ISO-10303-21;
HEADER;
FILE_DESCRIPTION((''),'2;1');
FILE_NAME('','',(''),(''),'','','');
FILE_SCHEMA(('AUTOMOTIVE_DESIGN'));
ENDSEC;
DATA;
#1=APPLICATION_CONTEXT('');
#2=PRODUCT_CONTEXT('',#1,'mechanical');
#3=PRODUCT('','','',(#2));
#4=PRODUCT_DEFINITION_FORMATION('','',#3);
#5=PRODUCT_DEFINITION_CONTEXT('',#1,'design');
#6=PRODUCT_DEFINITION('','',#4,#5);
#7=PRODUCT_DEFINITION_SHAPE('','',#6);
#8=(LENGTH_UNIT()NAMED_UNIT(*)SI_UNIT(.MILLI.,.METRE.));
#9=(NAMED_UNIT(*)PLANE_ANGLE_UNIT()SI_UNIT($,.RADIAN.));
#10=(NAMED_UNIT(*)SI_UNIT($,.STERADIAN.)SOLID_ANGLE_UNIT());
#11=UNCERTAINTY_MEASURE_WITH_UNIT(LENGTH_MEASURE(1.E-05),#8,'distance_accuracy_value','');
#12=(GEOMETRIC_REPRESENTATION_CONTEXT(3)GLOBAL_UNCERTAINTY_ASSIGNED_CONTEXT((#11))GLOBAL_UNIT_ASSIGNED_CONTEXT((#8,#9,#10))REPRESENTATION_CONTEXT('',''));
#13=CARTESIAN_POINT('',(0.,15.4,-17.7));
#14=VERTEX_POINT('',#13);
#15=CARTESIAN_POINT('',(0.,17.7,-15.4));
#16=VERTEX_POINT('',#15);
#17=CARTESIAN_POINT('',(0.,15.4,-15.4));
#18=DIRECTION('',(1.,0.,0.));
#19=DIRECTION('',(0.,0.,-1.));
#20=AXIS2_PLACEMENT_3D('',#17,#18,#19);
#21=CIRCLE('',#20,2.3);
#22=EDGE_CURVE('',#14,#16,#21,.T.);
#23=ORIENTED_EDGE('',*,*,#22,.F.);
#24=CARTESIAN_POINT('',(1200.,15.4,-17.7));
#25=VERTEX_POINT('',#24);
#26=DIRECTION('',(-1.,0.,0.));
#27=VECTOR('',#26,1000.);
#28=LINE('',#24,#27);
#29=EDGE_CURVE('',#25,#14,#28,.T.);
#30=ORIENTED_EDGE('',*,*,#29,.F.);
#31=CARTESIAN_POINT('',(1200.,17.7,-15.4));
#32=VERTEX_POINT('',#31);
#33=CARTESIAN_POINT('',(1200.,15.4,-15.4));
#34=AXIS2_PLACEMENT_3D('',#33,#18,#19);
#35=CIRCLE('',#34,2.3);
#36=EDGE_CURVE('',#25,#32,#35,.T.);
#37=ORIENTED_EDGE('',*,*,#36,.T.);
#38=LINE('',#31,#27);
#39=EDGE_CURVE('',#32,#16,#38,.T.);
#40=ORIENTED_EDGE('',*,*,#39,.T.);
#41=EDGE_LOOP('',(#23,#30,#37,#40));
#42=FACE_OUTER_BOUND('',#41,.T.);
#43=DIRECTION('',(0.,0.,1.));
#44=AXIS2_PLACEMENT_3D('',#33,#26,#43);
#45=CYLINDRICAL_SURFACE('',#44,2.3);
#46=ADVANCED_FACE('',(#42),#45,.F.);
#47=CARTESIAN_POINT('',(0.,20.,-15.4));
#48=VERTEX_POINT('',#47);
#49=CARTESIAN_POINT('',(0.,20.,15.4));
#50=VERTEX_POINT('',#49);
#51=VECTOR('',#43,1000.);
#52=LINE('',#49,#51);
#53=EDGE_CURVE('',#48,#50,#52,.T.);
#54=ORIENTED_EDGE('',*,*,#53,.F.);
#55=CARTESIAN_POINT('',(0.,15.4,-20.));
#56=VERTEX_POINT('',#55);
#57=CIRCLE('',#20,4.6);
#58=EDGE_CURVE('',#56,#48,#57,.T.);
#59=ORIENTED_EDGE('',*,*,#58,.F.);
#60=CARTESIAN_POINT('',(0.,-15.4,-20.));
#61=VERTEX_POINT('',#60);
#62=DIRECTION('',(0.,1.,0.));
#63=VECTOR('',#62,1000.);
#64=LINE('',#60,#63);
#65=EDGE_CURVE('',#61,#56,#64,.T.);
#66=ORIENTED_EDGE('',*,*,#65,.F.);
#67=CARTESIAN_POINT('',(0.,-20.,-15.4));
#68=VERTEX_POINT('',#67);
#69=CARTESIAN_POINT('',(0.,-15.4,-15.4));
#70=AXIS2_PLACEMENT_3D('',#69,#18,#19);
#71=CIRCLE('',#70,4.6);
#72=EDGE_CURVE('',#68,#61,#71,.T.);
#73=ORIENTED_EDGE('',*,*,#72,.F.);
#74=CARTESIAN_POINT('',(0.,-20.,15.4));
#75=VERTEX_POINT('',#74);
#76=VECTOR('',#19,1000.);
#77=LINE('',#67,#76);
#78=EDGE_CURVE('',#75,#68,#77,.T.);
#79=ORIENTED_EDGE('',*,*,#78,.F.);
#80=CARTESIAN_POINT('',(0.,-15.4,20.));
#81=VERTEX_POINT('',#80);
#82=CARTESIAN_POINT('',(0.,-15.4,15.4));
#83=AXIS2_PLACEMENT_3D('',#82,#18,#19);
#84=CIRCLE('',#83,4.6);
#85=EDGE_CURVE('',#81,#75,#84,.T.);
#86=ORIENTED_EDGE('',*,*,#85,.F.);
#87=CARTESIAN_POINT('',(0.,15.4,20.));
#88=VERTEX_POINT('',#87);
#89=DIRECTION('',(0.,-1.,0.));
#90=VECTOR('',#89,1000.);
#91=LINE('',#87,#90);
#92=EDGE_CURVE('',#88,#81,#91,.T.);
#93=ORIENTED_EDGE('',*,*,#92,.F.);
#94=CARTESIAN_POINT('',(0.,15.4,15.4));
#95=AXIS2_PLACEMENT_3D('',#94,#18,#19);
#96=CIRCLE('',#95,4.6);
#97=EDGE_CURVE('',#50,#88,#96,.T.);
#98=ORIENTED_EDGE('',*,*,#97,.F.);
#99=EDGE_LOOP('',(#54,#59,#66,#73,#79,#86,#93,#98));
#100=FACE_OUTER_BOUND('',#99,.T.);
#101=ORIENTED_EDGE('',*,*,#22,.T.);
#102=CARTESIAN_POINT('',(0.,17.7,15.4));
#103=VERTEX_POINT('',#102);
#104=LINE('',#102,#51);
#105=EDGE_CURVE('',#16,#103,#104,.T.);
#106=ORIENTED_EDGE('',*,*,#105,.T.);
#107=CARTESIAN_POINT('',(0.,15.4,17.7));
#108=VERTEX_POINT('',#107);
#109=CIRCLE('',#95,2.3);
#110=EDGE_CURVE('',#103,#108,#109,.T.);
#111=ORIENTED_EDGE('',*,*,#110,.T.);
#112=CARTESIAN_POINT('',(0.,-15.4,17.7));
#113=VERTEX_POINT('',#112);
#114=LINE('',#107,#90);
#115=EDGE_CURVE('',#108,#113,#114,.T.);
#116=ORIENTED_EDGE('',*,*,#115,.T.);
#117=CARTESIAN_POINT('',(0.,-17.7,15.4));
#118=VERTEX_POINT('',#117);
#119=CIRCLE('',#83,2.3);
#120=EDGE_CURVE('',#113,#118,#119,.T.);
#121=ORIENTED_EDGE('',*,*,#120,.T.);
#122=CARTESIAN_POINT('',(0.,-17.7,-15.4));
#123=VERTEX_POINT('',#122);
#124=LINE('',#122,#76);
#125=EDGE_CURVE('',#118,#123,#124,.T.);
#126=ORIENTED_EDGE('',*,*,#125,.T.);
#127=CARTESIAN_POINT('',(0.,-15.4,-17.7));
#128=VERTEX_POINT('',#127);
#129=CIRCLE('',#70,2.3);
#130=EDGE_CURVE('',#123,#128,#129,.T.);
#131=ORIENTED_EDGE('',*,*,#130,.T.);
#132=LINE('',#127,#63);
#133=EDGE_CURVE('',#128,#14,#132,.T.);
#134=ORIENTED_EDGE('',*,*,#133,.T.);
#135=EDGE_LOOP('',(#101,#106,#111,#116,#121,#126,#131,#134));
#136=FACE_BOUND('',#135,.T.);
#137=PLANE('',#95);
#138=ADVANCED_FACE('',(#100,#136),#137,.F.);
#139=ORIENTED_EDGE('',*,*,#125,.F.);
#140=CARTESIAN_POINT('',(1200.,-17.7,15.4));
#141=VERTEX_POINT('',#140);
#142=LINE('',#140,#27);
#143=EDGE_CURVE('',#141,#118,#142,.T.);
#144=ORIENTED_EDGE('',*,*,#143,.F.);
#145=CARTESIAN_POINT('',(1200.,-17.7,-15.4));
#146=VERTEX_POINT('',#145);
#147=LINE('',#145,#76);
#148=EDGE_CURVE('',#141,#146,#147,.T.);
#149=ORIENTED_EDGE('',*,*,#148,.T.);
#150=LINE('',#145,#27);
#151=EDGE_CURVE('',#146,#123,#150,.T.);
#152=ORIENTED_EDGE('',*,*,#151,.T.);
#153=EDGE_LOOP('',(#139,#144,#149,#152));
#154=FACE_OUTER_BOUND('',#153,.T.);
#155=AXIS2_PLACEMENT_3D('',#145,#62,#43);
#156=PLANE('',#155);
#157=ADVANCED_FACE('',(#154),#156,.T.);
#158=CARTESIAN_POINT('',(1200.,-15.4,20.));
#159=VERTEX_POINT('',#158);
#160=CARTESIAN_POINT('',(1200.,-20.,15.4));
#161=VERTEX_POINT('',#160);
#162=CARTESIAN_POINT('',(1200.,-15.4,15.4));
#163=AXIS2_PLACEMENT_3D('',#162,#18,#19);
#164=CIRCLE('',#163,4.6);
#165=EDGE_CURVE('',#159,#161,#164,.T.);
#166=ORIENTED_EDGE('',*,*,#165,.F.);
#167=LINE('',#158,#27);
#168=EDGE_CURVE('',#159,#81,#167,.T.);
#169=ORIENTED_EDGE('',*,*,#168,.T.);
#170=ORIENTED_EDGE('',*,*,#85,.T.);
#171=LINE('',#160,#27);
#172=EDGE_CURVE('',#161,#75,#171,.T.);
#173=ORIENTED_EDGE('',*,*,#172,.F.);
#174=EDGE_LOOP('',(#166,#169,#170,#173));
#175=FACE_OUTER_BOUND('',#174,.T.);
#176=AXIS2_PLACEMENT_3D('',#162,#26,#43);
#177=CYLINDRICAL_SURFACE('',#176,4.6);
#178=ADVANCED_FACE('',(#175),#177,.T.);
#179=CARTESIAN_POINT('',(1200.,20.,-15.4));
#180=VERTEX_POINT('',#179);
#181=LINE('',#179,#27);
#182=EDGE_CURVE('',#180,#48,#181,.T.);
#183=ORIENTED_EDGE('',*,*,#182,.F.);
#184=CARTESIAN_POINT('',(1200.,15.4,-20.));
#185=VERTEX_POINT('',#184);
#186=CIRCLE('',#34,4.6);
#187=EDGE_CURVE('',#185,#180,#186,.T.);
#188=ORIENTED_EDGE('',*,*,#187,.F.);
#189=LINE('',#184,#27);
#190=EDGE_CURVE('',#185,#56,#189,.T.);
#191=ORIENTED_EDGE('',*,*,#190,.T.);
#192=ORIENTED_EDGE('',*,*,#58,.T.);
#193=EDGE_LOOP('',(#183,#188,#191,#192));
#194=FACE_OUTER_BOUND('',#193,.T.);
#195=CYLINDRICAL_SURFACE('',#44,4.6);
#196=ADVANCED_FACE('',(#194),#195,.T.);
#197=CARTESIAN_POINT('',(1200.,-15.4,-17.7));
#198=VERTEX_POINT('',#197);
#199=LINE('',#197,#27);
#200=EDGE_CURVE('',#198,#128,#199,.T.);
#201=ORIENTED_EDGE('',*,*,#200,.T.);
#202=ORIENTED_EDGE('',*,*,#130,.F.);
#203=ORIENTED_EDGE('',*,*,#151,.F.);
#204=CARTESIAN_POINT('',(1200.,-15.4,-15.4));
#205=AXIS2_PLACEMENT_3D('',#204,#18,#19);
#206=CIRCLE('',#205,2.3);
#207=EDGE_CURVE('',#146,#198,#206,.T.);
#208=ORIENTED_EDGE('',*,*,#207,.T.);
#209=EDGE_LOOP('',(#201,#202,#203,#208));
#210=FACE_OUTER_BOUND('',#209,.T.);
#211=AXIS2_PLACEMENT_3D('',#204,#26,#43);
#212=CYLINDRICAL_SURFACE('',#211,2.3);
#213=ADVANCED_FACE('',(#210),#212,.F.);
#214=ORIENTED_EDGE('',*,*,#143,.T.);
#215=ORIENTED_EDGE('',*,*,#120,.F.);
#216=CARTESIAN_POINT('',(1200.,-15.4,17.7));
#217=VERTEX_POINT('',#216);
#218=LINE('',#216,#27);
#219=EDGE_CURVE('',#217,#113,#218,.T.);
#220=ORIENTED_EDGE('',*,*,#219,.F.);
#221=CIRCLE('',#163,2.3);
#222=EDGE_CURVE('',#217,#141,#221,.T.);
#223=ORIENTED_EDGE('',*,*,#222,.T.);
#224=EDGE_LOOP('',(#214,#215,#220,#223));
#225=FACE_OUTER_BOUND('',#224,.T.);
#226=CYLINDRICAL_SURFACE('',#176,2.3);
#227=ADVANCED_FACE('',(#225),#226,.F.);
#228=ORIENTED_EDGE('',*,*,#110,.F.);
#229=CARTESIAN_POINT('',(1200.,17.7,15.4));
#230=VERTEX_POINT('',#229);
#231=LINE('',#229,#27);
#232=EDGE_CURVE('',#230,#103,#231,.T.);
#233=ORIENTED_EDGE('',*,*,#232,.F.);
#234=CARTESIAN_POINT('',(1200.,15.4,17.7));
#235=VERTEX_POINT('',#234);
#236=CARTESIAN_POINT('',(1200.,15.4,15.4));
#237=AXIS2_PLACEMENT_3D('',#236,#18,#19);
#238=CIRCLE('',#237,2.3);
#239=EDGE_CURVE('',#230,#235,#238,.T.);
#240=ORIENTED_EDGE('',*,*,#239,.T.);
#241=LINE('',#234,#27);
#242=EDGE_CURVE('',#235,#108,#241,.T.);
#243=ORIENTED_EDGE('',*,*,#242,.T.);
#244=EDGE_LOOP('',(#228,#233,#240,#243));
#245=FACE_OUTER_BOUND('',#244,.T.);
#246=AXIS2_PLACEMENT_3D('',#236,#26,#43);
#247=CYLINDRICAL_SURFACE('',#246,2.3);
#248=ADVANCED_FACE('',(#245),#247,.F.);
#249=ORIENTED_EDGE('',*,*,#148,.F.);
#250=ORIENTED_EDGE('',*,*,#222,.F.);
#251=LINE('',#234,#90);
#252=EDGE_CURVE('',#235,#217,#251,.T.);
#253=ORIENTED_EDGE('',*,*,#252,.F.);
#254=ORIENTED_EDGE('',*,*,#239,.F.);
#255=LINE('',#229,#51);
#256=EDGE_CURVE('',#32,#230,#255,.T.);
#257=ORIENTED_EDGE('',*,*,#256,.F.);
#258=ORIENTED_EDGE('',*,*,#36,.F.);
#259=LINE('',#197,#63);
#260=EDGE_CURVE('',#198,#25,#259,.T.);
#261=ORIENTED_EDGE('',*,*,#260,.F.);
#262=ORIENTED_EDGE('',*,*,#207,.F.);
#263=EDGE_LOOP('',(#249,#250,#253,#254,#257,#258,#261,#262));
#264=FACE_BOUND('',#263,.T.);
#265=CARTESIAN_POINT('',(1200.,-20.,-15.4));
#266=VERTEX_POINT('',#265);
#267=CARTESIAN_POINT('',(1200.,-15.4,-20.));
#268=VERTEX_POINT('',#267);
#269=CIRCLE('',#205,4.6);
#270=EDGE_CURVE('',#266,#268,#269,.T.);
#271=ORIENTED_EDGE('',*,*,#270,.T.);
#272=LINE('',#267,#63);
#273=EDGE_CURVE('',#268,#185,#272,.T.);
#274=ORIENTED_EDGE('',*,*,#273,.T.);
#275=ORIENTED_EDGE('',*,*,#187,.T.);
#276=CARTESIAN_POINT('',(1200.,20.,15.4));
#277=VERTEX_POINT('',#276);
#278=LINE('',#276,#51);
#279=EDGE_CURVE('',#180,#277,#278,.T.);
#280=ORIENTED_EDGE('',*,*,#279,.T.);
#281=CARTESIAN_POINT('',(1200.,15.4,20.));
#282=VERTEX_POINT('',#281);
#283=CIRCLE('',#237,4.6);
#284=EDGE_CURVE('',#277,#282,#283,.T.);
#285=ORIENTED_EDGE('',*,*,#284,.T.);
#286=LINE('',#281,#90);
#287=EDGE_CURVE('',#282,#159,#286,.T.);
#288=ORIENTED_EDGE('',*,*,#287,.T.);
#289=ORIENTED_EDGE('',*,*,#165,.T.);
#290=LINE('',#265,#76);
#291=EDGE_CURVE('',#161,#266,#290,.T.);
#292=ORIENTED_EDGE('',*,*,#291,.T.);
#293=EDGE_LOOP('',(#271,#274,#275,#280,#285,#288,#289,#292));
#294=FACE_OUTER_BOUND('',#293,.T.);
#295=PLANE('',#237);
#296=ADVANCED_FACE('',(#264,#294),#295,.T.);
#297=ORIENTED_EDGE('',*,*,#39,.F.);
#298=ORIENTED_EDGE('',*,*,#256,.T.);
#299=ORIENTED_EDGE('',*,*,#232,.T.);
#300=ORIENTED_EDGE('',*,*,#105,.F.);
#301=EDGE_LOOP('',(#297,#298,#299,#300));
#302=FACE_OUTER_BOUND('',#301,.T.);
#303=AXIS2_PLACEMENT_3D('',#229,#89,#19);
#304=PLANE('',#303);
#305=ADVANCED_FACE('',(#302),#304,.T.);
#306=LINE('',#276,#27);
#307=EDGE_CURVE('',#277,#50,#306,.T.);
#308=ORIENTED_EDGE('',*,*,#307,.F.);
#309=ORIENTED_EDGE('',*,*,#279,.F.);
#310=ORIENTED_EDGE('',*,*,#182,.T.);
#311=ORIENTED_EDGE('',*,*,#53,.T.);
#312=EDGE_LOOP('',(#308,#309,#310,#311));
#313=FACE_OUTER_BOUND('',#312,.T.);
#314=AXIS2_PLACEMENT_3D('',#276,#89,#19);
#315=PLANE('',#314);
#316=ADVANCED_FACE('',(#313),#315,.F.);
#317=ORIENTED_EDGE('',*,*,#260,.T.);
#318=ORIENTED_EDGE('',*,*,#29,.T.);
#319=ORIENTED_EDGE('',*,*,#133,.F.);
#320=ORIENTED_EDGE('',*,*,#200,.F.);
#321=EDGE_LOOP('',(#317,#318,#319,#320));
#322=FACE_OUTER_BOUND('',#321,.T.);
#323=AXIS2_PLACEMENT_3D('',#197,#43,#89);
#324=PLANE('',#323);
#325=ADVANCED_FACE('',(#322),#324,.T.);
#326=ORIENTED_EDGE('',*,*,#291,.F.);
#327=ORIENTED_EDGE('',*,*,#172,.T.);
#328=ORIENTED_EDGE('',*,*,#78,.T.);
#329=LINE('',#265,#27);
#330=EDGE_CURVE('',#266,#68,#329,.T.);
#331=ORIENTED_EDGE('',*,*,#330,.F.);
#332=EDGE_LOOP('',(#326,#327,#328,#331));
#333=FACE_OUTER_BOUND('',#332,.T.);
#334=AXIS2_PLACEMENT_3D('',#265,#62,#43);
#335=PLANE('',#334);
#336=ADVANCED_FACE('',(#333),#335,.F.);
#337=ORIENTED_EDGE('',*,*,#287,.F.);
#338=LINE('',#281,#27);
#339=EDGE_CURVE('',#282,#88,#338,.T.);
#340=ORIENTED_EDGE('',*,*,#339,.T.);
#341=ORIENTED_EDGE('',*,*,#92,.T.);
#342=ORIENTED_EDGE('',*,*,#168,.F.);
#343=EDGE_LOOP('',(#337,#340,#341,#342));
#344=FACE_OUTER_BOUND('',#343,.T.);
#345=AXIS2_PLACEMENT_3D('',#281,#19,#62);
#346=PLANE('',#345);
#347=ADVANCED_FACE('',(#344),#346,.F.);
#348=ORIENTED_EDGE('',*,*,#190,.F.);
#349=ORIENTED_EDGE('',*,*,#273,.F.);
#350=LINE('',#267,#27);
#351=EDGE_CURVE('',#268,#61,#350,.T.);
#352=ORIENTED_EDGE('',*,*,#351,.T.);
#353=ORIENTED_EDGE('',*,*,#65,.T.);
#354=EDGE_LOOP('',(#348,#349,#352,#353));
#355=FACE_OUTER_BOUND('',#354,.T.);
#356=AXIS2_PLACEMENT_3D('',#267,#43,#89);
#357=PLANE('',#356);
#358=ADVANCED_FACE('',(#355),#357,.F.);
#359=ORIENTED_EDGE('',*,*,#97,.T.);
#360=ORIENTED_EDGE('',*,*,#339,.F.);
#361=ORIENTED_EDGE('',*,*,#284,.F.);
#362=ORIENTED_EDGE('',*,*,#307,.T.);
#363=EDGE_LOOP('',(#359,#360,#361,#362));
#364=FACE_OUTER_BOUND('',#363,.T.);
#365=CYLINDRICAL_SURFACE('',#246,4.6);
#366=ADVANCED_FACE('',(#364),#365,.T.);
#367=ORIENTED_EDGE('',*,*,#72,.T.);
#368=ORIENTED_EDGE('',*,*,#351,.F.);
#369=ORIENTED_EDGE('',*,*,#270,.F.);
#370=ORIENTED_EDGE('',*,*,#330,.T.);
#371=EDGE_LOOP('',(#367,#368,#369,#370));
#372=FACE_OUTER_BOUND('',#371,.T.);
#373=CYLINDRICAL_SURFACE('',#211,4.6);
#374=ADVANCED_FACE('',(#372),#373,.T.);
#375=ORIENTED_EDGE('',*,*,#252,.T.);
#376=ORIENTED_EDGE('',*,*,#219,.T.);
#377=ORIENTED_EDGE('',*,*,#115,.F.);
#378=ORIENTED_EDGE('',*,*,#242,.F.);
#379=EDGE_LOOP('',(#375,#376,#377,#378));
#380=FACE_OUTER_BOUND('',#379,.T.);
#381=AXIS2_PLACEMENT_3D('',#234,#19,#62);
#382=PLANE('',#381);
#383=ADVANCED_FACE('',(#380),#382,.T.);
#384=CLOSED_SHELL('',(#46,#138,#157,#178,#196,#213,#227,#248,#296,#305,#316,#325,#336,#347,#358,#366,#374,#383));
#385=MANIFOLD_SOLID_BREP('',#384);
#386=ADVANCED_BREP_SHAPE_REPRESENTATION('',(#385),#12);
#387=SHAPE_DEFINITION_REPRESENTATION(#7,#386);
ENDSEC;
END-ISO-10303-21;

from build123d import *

# Parameters (mm, degrees)
SQUARE_TUBE_40_X_40_X_2_3_1_DEPTH = 1200


with BuildPart() as part:
    # Sketch11 → Square Tube 40 X 40 X 2.3(1) (new body)
    with BuildSketch(Plane.YZ):
        with BuildLine():
            Line((-15.4, -20), (15.4, -20))
            ThreePointArc((15.4, -20), (18.652691193, -18.652691193), (20, -15.4))
            Line((20, -15.4), (20, 15.4))
            ThreePointArc((20, 15.4), (18.652691193, 18.652691193), (15.4, 20))
            Line((15.4, 20), (-15.4, 20))
            ThreePointArc((-15.4, 20), (-18.652691193, 18.652691193), (-20, 15.4))
            Line((-20, 15.4), (-20, -15.4))
            ThreePointArc((-20, -15.4), (-18.652691193, -18.652691193), (-15.4, -20))
        make_face()
        with BuildLine():
            Line((-15.4, -17.7), (15.4, -17.7))
            ThreePointArc((15.4, -17.7), (17.026345597, -17.026345597), (17.7, -15.4))
            Line((17.7, -15.4), (17.7, 15.4))
            ThreePointArc((17.7, 15.4), (17.026345597, 17.026345597), (15.4, 17.7))
            Line((15.4, 17.7), (-15.4, 17.7))
            ThreePointArc((-15.4, 17.7), (-17.026345597, 17.026345597), (-17.7, 15.4))
            Line((-17.7, 15.4), (-17.7, -15.4))
            ThreePointArc((-17.7, -15.4), (-17.026345597, -17.026345597), (-15.4, -17.7))
        make_face(mode=Mode.SUBTRACT)
    extrude(amount=SQUARE_TUBE_40_X_40_X_2_3_1_DEPTH)


solid = part.part
